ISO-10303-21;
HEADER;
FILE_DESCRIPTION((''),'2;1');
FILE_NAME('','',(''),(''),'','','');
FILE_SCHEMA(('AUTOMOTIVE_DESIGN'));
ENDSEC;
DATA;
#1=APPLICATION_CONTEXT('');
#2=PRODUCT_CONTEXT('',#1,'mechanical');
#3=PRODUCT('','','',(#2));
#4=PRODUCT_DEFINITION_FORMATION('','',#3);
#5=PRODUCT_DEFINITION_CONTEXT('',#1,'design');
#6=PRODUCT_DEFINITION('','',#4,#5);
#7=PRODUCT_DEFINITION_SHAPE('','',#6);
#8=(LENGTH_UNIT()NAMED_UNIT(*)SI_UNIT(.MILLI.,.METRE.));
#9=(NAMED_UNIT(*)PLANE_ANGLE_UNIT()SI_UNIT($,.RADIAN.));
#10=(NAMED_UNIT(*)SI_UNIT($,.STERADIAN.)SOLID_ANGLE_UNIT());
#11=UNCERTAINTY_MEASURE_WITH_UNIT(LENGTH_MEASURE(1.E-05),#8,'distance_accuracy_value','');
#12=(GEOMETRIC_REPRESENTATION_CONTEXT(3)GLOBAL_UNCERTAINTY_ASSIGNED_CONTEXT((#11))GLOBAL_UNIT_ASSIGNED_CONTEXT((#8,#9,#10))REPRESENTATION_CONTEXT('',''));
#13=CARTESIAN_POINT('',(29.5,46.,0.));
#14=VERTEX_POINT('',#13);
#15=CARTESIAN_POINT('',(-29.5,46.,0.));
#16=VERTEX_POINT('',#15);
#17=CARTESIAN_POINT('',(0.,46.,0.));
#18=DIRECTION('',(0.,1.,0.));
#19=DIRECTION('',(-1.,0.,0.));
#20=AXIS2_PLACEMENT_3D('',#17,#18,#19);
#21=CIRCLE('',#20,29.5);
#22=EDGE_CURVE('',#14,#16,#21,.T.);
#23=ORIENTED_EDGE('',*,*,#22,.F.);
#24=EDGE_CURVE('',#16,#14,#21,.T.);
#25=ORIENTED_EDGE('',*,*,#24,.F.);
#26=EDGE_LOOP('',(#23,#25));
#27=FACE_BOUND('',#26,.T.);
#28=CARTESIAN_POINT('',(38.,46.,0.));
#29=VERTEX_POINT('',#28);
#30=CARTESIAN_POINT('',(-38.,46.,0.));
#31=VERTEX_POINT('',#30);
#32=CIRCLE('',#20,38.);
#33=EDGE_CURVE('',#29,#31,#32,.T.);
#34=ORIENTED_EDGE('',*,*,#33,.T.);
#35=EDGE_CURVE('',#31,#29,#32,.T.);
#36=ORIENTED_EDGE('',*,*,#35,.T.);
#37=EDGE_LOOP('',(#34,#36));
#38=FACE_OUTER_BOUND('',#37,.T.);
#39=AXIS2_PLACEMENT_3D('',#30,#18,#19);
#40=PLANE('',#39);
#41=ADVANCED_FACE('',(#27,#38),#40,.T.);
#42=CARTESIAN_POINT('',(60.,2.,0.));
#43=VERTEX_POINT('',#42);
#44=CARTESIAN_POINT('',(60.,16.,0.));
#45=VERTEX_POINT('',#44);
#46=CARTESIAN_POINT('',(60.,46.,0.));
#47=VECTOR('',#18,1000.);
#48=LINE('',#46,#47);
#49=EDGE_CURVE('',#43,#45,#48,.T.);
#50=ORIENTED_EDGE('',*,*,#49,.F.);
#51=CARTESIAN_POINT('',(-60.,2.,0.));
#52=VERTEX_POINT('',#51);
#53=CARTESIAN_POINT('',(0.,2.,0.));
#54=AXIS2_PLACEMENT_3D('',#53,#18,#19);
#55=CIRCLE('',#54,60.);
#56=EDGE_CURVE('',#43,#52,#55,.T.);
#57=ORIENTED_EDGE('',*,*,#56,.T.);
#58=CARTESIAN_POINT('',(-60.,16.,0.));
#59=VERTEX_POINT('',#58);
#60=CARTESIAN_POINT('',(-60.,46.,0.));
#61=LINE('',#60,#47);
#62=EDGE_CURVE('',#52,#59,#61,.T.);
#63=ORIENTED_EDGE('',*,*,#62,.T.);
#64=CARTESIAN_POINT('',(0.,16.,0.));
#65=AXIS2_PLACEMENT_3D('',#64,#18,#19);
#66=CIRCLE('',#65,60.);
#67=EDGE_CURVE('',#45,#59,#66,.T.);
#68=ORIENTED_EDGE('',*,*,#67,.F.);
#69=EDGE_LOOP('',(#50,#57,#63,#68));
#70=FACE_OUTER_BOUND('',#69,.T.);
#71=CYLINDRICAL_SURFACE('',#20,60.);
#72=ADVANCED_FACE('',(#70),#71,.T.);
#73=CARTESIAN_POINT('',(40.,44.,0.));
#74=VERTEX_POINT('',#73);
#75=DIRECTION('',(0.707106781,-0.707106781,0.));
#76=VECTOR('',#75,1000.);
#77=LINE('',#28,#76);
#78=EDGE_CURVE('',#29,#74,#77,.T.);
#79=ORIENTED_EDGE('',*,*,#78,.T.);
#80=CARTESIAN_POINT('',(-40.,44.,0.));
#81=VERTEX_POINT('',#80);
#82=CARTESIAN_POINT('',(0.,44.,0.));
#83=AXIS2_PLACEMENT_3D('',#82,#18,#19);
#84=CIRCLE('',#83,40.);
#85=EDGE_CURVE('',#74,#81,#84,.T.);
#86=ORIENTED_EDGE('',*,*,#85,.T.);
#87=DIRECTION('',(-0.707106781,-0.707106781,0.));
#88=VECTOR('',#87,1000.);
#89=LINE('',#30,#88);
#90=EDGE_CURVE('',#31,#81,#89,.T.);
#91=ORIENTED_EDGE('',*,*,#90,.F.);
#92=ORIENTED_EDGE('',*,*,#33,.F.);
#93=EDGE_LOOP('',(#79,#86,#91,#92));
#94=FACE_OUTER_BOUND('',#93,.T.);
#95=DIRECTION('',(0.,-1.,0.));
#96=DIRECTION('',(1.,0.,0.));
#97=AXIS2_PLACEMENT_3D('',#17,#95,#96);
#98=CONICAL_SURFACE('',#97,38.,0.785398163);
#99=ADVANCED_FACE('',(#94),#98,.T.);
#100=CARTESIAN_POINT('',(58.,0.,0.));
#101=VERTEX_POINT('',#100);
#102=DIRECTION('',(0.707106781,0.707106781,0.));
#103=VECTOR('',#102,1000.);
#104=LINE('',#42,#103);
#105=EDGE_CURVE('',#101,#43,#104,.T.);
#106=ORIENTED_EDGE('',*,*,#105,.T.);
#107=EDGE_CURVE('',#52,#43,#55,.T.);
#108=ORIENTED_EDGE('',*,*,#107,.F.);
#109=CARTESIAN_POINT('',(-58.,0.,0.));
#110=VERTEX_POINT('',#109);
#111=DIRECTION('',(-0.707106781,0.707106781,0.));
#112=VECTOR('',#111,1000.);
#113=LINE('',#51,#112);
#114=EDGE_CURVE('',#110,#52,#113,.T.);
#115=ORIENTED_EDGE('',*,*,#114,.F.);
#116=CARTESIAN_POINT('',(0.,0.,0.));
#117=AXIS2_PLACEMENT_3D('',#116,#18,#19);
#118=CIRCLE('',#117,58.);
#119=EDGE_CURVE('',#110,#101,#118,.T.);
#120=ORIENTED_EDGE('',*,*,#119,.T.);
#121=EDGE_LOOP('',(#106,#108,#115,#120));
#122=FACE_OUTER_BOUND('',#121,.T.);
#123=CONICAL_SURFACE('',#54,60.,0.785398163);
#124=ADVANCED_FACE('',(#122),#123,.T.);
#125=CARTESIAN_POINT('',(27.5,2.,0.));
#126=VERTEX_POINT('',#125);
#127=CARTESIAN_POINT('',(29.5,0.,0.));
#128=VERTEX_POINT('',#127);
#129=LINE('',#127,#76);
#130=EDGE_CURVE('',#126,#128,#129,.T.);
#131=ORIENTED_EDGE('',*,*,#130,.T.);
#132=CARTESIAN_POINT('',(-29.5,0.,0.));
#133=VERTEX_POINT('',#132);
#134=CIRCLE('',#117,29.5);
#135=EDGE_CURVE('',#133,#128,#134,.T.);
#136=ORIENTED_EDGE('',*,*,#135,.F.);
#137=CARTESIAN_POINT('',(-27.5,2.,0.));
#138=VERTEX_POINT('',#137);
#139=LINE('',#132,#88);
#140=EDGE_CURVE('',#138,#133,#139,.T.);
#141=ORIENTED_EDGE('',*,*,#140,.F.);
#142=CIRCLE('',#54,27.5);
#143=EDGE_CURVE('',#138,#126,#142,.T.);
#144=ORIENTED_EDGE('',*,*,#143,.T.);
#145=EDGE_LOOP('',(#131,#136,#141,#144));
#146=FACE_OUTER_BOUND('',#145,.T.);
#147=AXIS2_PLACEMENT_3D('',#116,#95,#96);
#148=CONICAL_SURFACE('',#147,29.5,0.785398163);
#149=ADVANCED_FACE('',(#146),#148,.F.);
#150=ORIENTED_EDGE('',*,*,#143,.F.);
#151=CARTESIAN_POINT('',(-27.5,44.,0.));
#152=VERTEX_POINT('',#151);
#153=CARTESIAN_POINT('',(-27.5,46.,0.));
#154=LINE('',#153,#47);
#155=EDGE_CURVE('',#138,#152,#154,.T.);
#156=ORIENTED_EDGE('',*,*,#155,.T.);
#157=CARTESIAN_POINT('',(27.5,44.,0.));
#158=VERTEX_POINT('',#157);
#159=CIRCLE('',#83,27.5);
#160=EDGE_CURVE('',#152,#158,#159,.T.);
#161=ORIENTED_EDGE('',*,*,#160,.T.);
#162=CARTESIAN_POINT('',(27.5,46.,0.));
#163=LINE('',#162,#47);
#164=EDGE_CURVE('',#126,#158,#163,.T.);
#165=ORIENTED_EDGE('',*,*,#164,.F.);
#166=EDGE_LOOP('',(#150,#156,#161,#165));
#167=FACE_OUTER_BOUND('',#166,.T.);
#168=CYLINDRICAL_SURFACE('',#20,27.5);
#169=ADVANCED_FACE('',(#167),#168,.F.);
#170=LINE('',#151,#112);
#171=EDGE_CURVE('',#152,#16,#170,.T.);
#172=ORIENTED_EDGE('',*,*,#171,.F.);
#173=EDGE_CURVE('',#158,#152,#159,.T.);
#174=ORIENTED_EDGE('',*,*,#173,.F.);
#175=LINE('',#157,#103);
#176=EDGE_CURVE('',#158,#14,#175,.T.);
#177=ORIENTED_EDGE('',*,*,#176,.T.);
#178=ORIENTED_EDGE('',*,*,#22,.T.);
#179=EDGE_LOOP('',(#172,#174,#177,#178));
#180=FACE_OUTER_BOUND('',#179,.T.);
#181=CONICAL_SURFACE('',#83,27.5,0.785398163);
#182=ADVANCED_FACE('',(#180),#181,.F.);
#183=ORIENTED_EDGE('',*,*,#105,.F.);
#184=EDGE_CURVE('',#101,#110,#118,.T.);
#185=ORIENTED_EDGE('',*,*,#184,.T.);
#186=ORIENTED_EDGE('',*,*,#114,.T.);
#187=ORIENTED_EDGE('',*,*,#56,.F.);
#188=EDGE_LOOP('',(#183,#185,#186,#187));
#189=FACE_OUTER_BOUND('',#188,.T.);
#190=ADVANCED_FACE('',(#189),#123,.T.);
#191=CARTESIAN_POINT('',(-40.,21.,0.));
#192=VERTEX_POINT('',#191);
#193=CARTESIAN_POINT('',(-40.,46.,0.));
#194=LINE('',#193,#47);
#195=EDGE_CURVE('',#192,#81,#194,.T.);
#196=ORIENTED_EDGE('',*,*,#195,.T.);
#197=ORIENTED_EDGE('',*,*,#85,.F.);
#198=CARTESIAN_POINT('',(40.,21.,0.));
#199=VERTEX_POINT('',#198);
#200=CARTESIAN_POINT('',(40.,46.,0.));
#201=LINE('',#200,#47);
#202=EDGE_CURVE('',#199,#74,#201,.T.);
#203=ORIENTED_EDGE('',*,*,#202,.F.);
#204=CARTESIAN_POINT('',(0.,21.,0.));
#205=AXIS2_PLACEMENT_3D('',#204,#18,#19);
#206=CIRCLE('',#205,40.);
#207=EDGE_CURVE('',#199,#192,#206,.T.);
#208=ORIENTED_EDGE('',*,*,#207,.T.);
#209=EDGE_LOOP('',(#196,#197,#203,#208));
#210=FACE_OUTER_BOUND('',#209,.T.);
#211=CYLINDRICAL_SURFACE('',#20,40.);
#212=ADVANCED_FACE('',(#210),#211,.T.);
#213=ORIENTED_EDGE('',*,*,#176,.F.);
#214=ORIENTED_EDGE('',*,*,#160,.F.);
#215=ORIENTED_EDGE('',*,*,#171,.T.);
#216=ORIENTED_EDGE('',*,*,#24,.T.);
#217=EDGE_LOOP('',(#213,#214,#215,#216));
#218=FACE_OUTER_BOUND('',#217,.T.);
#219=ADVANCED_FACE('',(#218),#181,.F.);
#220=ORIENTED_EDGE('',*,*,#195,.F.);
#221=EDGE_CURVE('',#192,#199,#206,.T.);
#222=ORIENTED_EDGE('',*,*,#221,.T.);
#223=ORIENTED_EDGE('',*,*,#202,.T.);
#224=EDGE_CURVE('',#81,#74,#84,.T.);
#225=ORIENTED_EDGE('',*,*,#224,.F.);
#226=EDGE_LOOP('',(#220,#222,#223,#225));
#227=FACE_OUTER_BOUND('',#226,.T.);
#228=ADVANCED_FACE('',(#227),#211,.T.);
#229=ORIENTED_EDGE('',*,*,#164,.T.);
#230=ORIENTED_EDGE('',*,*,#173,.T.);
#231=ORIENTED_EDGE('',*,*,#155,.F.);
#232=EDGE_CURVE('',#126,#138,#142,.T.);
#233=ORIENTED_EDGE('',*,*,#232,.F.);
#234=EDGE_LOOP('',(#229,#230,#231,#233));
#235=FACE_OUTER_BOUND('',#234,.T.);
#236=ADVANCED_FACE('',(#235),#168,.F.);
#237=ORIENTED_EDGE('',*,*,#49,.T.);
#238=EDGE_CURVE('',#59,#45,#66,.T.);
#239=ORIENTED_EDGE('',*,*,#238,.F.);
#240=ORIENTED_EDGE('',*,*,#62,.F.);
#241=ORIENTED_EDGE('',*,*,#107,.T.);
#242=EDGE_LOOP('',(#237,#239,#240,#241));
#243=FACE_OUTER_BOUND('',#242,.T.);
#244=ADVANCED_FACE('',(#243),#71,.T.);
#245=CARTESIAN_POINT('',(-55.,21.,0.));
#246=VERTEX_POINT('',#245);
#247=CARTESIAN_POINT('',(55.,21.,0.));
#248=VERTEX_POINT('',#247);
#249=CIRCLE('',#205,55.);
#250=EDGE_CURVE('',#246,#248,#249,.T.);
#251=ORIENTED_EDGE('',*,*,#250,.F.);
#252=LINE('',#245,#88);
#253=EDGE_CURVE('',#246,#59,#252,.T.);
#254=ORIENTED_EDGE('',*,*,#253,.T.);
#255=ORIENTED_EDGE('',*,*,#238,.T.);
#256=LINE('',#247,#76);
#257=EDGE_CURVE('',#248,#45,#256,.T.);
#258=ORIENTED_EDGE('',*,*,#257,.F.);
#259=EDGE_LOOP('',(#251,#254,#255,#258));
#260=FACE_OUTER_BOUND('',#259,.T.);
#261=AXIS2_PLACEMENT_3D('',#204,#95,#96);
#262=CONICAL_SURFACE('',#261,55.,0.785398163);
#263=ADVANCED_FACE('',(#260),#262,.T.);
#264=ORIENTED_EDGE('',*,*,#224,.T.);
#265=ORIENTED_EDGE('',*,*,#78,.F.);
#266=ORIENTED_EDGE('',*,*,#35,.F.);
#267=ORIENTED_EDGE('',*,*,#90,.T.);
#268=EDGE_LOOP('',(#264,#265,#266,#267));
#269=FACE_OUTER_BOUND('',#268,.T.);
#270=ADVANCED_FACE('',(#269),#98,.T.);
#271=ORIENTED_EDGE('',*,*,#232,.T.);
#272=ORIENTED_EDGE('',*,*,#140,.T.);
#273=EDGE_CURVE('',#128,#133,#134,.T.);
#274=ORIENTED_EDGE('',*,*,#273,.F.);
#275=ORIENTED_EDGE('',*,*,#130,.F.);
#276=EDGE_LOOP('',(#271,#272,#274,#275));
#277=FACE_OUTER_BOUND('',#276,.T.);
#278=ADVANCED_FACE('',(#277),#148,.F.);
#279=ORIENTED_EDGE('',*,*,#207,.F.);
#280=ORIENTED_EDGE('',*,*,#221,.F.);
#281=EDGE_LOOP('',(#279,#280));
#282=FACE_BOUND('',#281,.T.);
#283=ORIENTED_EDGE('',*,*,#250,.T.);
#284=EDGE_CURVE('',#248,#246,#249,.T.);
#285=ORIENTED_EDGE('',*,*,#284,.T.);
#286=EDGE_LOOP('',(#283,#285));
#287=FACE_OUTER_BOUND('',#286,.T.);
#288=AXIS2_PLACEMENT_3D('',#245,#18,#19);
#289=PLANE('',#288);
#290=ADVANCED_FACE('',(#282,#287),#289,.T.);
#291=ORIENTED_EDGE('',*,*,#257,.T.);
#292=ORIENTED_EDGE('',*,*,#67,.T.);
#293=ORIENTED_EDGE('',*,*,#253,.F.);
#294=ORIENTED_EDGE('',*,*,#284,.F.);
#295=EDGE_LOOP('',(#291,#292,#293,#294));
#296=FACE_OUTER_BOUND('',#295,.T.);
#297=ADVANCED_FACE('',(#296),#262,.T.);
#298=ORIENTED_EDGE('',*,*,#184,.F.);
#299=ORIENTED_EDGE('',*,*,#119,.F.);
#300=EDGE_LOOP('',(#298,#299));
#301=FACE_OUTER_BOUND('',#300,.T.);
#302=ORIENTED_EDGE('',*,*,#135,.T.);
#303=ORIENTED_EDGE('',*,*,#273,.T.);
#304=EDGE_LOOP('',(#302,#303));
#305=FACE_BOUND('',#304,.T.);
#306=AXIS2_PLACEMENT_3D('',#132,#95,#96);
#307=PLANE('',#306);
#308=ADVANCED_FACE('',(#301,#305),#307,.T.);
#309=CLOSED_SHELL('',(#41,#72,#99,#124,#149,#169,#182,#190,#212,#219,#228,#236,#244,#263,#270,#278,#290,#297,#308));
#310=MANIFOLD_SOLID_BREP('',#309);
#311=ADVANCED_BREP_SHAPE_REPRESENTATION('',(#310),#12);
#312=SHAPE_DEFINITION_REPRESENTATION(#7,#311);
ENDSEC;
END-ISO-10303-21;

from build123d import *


with BuildPart() as part:
    # Sketch1 → Revolve1 (revolve)
    with BuildSketch(Plane.XY):
        Polygon((-29.5, 0), (-58, 0), (-60, 2), (-60, 16), (-55, 21), (-40, 21), (-40, 44), (-38, 46), (-29.5, 46), (-27.5, 44), (-27.5, 2), align=None)
    revolve(axis=Axis((0, 46, 0), (0, -1, 0)))


solid = part.part
